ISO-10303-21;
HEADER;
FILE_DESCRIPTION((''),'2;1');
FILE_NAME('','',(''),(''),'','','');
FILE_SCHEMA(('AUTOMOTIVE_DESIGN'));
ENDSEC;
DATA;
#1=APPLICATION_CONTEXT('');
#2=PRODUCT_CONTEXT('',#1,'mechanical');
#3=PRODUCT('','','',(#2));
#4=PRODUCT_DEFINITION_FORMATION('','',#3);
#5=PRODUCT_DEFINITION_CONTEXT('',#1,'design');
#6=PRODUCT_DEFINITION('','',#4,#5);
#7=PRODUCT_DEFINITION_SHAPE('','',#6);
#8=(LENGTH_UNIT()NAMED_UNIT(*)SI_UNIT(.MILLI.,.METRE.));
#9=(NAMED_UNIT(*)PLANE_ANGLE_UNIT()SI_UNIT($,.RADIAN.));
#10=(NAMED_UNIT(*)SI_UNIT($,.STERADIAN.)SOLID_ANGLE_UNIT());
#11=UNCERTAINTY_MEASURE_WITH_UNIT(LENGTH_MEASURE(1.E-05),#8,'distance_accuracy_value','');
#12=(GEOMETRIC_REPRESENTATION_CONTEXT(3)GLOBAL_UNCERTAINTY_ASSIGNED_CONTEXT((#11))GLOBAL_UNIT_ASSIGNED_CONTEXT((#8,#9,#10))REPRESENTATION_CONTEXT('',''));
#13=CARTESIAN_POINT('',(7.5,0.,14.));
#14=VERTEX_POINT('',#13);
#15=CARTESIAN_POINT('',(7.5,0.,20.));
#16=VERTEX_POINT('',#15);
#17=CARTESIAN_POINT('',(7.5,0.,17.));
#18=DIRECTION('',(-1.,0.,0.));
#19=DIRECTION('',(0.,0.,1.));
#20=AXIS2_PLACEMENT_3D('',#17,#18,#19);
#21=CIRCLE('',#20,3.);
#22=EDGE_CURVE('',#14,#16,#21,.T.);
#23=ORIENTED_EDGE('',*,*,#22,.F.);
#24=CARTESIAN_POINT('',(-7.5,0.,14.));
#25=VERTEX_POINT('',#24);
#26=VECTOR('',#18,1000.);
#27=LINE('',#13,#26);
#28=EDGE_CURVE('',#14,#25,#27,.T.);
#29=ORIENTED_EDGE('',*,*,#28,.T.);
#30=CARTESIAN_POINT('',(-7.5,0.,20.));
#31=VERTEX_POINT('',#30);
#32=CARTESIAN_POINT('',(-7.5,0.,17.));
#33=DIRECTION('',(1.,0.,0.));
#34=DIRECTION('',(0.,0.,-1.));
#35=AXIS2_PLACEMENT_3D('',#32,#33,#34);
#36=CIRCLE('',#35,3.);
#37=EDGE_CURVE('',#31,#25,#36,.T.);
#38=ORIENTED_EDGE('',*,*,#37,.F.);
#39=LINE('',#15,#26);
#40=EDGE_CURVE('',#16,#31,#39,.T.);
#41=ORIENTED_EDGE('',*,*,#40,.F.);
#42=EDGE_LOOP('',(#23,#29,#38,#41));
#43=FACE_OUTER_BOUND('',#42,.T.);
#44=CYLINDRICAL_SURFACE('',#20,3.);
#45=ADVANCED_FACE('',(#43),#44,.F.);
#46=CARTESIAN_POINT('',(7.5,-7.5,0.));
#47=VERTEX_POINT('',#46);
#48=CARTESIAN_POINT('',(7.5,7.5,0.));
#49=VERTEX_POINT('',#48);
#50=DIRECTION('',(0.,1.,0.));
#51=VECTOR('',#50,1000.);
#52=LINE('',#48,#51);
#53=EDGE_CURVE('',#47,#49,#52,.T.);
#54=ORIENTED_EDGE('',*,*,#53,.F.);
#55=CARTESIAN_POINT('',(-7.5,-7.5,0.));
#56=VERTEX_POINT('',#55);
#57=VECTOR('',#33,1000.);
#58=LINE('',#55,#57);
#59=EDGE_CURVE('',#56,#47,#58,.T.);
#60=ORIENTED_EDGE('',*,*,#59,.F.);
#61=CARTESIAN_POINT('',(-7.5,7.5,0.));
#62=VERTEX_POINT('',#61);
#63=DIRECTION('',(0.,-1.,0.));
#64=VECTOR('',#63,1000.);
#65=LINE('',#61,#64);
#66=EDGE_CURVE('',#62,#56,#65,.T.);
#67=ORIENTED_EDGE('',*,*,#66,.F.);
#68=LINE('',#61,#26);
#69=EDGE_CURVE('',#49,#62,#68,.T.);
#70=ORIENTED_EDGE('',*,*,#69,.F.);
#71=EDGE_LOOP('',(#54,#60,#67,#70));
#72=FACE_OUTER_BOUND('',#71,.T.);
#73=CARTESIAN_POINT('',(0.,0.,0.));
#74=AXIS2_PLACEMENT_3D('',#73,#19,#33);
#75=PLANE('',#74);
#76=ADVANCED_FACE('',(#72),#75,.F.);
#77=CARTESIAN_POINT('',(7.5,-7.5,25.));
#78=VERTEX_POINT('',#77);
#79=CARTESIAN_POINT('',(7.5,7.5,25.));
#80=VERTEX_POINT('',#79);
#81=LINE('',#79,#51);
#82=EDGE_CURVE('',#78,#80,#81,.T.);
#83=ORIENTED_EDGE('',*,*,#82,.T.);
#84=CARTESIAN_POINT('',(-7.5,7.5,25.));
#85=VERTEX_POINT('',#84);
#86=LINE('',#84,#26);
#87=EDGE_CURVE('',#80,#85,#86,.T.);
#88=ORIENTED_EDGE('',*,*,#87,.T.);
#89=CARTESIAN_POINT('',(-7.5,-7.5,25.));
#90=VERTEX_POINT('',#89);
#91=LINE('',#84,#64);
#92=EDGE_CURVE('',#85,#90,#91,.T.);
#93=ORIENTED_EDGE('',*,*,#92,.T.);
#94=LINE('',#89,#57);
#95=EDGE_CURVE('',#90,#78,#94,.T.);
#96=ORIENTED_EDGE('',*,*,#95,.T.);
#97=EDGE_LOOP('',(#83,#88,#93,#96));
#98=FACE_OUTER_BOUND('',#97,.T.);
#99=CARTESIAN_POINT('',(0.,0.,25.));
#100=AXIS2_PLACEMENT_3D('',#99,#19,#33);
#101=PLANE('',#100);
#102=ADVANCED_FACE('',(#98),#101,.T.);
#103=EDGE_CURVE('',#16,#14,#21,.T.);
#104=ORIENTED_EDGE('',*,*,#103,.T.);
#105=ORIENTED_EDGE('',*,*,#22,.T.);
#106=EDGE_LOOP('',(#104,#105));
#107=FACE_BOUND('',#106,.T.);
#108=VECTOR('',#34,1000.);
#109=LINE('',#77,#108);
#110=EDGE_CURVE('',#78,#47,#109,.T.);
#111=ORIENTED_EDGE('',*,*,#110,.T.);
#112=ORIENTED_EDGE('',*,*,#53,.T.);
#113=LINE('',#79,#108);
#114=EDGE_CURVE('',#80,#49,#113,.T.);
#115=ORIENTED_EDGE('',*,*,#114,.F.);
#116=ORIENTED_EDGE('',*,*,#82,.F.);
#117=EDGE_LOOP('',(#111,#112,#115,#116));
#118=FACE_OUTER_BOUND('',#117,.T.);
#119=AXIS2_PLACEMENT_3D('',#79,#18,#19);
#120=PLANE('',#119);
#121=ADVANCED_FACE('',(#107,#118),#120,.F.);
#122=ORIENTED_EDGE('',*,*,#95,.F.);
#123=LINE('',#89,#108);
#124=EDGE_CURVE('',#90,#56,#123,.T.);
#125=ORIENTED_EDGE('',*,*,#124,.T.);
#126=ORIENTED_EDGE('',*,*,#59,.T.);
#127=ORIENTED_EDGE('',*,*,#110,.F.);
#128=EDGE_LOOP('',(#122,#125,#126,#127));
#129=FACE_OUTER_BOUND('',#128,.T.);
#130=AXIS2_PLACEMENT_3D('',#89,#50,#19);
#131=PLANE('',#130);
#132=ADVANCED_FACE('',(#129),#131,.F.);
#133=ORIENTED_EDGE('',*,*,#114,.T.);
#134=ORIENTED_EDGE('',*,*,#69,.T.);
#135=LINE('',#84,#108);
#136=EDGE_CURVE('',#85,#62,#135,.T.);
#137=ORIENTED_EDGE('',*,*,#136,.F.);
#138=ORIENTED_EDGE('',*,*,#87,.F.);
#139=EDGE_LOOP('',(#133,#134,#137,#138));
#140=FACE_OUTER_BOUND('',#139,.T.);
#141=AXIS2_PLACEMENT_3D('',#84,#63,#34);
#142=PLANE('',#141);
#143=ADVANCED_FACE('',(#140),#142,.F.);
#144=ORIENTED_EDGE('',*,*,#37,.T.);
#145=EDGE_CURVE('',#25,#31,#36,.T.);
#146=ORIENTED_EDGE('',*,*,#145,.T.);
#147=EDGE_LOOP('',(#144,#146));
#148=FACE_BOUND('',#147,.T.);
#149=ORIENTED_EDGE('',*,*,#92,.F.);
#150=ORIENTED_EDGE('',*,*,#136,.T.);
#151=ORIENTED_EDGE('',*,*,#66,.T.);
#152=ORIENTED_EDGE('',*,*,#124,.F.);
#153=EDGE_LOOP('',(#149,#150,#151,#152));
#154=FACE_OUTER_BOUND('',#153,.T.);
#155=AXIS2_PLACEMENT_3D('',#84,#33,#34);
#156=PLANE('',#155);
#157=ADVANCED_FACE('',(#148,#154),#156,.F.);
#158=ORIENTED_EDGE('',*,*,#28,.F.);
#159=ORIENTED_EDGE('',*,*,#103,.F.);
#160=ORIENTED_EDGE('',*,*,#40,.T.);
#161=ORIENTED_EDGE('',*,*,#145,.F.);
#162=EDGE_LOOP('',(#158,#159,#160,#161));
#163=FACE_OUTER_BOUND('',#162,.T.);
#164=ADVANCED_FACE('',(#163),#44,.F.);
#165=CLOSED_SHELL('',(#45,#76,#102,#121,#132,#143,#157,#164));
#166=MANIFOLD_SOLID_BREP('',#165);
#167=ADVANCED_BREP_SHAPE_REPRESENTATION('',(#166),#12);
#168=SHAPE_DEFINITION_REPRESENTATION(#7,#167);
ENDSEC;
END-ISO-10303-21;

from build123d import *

# Parameters (mm, degrees)
SKETCH1_W               = 15
SKETCH1_H               = 15
BOSS_EXTRUDE1_DEPTH     = 25
CUT_EXTRUDE1_DEPTH      = 31.103986447
CUT_EXTRUDE1_DEPTH_BACK = 31.103986447
SKETCH2_R               = 3


with BuildPart() as part:
    # Sketch1 → Boss-Extrude1 (new body)
    with BuildSketch(Plane.XY):
        Rectangle(SKETCH1_W, SKETCH1_H)
    extrude(amount=BOSS_EXTRUDE1_DEPTH)

    # Sketch2 → Cut-Extrude1 (cut, two sides: drawn at the far end of the back side and taken through both)
    with BuildSketch(Plane.ZY.offset(7.5).offset(-CUT_EXTRUDE1_DEPTH_BACK)):
        with Locations((17, 0)):
            Circle(SKETCH2_R)
    extrude(amount=CUT_EXTRUDE1_DEPTH + CUT_EXTRUDE1_DEPTH_BACK, mode=Mode.SUBTRACT)


solid = part.part
